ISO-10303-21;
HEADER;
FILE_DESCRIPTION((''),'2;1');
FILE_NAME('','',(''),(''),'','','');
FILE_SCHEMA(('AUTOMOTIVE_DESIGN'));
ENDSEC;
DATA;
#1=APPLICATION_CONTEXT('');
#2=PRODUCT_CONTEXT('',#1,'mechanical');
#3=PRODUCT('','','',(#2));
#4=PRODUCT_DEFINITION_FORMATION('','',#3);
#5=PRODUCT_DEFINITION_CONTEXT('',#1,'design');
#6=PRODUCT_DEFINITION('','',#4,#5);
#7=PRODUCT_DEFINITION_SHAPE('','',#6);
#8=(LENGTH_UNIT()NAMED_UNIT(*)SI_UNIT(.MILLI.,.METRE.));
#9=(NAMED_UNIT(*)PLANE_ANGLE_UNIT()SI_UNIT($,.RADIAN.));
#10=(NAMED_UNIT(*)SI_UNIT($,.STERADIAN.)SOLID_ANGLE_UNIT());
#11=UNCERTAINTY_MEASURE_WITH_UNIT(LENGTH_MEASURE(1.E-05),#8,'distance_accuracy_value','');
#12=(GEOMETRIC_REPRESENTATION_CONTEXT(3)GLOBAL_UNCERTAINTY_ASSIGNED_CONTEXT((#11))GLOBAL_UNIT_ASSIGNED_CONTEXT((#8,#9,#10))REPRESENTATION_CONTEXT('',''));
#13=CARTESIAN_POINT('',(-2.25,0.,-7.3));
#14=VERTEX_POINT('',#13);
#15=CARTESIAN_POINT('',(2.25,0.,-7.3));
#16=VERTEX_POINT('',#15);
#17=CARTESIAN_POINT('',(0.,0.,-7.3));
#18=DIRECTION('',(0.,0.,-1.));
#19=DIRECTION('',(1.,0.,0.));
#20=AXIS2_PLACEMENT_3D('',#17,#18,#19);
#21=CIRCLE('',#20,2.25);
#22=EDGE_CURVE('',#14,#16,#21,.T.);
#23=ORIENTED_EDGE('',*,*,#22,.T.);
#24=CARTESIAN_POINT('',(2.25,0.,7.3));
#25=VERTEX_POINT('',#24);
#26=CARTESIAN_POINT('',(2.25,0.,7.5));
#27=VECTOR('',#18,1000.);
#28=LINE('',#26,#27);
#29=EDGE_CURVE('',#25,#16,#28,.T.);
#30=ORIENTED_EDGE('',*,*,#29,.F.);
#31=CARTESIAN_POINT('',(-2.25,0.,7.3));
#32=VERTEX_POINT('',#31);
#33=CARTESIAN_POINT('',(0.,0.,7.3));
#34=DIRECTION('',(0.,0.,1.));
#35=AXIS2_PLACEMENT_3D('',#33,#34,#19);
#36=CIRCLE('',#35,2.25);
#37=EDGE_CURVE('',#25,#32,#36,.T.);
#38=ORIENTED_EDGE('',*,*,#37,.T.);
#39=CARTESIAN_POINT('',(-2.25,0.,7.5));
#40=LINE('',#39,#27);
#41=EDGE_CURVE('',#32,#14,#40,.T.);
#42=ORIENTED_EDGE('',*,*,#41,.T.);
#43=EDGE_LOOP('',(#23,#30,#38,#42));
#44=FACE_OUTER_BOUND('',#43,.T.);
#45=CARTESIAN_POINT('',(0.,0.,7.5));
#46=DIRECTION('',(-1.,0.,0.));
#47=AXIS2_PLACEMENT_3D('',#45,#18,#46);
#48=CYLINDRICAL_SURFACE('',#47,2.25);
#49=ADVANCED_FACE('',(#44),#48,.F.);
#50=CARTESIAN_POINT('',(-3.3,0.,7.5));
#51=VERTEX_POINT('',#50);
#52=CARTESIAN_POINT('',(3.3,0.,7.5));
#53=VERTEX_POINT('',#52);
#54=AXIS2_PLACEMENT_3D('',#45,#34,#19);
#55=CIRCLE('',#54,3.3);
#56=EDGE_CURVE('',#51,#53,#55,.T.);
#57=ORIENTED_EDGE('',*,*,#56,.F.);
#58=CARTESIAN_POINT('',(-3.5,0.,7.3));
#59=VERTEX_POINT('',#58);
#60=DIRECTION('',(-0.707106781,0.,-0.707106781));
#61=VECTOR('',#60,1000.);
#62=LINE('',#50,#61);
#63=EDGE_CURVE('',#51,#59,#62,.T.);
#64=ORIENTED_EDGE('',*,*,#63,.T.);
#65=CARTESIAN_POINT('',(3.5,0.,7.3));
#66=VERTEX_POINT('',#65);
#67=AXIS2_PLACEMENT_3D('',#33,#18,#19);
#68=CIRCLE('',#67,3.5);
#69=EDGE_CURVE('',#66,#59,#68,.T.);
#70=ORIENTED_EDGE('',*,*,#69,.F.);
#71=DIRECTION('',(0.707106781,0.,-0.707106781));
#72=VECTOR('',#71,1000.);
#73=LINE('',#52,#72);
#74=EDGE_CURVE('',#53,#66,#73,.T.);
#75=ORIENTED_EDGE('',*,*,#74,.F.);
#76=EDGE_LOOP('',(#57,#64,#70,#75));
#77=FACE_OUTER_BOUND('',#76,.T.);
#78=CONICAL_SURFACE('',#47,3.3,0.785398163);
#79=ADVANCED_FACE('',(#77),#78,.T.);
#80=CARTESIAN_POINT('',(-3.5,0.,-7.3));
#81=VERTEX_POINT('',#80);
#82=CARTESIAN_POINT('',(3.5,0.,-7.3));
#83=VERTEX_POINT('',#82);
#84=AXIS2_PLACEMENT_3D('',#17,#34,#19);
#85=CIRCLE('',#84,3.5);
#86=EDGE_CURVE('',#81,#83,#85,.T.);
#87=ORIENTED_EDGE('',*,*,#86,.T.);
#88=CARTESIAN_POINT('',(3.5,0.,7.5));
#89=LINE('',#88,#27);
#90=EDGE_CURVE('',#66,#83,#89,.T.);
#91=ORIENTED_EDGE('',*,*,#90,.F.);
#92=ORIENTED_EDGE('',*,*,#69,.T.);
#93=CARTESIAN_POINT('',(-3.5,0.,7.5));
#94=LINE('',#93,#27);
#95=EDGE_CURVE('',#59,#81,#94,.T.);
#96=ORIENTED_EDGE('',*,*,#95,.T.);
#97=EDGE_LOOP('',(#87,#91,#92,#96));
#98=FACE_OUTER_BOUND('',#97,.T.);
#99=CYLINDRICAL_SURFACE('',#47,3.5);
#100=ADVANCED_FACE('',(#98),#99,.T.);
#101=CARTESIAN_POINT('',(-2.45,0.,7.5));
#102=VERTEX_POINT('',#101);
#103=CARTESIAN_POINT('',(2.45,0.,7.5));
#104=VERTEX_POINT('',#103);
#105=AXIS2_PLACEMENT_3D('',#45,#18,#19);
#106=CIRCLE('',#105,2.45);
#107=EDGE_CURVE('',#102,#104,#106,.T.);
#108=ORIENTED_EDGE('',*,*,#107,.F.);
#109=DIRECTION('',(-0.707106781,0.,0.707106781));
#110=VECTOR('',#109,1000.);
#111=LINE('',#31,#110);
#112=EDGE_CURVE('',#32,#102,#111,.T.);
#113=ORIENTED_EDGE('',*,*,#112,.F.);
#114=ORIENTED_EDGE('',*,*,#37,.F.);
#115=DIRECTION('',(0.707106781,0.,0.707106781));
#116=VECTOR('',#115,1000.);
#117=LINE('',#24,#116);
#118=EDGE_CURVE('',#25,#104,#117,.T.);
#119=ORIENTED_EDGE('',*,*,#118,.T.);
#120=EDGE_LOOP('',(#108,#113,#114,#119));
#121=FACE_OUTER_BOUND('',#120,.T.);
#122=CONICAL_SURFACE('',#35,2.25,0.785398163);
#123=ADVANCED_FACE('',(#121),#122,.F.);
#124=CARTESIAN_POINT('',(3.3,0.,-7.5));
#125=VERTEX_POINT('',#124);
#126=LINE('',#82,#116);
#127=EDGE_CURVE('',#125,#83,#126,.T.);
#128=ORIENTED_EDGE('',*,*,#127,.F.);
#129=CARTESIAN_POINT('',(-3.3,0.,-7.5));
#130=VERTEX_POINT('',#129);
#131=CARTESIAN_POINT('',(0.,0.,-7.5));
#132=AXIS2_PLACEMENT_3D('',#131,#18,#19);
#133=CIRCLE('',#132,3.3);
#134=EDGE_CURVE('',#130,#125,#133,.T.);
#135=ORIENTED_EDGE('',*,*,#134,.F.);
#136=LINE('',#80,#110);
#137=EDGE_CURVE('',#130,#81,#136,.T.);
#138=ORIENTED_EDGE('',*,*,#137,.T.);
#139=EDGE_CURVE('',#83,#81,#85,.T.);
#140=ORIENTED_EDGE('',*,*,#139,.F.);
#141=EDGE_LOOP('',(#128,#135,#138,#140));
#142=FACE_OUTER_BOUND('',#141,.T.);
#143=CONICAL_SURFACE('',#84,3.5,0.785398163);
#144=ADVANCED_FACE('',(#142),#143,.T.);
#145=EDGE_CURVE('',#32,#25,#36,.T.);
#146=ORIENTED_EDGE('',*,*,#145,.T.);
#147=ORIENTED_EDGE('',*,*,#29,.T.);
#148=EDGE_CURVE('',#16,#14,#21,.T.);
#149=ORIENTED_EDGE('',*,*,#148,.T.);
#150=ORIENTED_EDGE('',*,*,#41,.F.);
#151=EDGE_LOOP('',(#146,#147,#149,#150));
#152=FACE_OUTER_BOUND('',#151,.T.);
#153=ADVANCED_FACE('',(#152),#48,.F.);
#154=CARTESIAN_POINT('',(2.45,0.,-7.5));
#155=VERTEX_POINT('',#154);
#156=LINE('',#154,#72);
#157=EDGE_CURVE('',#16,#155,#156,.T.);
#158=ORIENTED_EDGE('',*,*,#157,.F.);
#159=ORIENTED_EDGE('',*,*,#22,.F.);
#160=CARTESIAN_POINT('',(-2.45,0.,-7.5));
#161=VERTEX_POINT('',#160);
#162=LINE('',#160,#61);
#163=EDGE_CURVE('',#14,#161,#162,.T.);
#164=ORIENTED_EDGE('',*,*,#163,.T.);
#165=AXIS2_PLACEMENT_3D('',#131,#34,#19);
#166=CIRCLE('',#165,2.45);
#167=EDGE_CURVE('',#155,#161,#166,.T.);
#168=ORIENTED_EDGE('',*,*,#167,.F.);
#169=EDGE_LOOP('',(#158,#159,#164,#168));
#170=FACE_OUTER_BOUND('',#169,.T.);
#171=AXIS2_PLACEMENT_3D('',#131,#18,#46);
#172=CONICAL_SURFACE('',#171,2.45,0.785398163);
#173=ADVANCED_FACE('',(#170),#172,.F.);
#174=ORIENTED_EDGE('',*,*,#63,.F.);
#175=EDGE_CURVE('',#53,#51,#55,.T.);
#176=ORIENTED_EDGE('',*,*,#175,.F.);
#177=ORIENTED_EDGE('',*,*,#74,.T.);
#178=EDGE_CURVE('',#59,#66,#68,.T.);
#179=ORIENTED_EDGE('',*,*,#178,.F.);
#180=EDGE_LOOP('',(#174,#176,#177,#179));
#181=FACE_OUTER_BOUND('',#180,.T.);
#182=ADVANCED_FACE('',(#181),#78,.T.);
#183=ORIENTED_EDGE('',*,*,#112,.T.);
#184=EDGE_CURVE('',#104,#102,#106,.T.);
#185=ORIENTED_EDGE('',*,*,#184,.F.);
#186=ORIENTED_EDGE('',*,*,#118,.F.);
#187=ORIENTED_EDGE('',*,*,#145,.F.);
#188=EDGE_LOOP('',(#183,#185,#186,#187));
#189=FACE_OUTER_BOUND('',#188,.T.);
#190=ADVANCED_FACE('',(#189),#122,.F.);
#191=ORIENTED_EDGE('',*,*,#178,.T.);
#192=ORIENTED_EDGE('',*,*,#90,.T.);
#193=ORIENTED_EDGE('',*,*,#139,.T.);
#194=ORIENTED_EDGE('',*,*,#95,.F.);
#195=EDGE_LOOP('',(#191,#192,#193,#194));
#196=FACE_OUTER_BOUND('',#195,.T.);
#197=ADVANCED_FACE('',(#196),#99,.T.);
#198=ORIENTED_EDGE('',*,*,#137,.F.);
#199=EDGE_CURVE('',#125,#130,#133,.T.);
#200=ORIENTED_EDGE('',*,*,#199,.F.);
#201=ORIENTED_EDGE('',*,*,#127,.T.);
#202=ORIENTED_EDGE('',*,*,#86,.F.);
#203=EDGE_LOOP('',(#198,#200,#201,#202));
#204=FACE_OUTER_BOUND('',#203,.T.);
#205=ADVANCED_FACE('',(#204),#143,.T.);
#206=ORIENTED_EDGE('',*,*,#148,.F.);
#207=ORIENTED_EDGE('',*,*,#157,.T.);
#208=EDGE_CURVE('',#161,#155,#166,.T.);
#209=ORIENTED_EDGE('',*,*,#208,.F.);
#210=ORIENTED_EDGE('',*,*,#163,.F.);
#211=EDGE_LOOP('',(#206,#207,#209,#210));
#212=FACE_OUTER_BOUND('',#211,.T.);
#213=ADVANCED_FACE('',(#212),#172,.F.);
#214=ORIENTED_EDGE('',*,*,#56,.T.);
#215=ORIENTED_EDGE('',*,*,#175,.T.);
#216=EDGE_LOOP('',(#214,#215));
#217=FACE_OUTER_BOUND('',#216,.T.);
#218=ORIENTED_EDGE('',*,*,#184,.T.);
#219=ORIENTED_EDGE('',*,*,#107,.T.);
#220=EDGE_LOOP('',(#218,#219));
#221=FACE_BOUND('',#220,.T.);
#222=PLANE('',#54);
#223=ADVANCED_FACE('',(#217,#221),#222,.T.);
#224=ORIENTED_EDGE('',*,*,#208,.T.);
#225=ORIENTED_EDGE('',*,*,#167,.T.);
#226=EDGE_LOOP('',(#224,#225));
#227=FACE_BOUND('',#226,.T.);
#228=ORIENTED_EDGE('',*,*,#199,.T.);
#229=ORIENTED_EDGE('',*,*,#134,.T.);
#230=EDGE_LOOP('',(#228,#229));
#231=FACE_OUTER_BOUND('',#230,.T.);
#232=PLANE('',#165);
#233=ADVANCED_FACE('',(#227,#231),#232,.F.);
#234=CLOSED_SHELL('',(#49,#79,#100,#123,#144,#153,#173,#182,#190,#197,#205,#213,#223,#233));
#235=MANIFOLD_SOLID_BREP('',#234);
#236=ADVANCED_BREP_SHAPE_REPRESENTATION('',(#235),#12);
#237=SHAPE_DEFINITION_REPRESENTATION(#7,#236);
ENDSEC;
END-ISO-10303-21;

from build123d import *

# Parameters (mm, degrees)
SKETCH1_R           = 3.5
SKETCH1_R_2         = 2.25
BOSS_EXTRUDE1_DEPTH = 7.5
CHAMFER1_SIZE       = 0.2


with BuildPart() as part:
    # Sketch1 → Boss-Extrude1 (new, symmetric)
    with BuildSketch(Plane.XY):
        Circle(SKETCH1_R)
        Circle(SKETCH1_R_2, mode=Mode.SUBTRACT)
    extrude(amount=BOSS_EXTRUDE1_DEPTH, both=True)

    # Chamfer1
    chamfer1_edges = [part.edges().sort_by_distance(p)[0] for p in [
        (-3.5, 0, -7.5),
        (-3.5, 0, 7.5),
        (-2.25, 0, -7.5),
        (-2.25, 0, 7.5),
    ]]
    chamfer(chamfer1_edges, length=CHAMFER1_SIZE)


solid = part.part
